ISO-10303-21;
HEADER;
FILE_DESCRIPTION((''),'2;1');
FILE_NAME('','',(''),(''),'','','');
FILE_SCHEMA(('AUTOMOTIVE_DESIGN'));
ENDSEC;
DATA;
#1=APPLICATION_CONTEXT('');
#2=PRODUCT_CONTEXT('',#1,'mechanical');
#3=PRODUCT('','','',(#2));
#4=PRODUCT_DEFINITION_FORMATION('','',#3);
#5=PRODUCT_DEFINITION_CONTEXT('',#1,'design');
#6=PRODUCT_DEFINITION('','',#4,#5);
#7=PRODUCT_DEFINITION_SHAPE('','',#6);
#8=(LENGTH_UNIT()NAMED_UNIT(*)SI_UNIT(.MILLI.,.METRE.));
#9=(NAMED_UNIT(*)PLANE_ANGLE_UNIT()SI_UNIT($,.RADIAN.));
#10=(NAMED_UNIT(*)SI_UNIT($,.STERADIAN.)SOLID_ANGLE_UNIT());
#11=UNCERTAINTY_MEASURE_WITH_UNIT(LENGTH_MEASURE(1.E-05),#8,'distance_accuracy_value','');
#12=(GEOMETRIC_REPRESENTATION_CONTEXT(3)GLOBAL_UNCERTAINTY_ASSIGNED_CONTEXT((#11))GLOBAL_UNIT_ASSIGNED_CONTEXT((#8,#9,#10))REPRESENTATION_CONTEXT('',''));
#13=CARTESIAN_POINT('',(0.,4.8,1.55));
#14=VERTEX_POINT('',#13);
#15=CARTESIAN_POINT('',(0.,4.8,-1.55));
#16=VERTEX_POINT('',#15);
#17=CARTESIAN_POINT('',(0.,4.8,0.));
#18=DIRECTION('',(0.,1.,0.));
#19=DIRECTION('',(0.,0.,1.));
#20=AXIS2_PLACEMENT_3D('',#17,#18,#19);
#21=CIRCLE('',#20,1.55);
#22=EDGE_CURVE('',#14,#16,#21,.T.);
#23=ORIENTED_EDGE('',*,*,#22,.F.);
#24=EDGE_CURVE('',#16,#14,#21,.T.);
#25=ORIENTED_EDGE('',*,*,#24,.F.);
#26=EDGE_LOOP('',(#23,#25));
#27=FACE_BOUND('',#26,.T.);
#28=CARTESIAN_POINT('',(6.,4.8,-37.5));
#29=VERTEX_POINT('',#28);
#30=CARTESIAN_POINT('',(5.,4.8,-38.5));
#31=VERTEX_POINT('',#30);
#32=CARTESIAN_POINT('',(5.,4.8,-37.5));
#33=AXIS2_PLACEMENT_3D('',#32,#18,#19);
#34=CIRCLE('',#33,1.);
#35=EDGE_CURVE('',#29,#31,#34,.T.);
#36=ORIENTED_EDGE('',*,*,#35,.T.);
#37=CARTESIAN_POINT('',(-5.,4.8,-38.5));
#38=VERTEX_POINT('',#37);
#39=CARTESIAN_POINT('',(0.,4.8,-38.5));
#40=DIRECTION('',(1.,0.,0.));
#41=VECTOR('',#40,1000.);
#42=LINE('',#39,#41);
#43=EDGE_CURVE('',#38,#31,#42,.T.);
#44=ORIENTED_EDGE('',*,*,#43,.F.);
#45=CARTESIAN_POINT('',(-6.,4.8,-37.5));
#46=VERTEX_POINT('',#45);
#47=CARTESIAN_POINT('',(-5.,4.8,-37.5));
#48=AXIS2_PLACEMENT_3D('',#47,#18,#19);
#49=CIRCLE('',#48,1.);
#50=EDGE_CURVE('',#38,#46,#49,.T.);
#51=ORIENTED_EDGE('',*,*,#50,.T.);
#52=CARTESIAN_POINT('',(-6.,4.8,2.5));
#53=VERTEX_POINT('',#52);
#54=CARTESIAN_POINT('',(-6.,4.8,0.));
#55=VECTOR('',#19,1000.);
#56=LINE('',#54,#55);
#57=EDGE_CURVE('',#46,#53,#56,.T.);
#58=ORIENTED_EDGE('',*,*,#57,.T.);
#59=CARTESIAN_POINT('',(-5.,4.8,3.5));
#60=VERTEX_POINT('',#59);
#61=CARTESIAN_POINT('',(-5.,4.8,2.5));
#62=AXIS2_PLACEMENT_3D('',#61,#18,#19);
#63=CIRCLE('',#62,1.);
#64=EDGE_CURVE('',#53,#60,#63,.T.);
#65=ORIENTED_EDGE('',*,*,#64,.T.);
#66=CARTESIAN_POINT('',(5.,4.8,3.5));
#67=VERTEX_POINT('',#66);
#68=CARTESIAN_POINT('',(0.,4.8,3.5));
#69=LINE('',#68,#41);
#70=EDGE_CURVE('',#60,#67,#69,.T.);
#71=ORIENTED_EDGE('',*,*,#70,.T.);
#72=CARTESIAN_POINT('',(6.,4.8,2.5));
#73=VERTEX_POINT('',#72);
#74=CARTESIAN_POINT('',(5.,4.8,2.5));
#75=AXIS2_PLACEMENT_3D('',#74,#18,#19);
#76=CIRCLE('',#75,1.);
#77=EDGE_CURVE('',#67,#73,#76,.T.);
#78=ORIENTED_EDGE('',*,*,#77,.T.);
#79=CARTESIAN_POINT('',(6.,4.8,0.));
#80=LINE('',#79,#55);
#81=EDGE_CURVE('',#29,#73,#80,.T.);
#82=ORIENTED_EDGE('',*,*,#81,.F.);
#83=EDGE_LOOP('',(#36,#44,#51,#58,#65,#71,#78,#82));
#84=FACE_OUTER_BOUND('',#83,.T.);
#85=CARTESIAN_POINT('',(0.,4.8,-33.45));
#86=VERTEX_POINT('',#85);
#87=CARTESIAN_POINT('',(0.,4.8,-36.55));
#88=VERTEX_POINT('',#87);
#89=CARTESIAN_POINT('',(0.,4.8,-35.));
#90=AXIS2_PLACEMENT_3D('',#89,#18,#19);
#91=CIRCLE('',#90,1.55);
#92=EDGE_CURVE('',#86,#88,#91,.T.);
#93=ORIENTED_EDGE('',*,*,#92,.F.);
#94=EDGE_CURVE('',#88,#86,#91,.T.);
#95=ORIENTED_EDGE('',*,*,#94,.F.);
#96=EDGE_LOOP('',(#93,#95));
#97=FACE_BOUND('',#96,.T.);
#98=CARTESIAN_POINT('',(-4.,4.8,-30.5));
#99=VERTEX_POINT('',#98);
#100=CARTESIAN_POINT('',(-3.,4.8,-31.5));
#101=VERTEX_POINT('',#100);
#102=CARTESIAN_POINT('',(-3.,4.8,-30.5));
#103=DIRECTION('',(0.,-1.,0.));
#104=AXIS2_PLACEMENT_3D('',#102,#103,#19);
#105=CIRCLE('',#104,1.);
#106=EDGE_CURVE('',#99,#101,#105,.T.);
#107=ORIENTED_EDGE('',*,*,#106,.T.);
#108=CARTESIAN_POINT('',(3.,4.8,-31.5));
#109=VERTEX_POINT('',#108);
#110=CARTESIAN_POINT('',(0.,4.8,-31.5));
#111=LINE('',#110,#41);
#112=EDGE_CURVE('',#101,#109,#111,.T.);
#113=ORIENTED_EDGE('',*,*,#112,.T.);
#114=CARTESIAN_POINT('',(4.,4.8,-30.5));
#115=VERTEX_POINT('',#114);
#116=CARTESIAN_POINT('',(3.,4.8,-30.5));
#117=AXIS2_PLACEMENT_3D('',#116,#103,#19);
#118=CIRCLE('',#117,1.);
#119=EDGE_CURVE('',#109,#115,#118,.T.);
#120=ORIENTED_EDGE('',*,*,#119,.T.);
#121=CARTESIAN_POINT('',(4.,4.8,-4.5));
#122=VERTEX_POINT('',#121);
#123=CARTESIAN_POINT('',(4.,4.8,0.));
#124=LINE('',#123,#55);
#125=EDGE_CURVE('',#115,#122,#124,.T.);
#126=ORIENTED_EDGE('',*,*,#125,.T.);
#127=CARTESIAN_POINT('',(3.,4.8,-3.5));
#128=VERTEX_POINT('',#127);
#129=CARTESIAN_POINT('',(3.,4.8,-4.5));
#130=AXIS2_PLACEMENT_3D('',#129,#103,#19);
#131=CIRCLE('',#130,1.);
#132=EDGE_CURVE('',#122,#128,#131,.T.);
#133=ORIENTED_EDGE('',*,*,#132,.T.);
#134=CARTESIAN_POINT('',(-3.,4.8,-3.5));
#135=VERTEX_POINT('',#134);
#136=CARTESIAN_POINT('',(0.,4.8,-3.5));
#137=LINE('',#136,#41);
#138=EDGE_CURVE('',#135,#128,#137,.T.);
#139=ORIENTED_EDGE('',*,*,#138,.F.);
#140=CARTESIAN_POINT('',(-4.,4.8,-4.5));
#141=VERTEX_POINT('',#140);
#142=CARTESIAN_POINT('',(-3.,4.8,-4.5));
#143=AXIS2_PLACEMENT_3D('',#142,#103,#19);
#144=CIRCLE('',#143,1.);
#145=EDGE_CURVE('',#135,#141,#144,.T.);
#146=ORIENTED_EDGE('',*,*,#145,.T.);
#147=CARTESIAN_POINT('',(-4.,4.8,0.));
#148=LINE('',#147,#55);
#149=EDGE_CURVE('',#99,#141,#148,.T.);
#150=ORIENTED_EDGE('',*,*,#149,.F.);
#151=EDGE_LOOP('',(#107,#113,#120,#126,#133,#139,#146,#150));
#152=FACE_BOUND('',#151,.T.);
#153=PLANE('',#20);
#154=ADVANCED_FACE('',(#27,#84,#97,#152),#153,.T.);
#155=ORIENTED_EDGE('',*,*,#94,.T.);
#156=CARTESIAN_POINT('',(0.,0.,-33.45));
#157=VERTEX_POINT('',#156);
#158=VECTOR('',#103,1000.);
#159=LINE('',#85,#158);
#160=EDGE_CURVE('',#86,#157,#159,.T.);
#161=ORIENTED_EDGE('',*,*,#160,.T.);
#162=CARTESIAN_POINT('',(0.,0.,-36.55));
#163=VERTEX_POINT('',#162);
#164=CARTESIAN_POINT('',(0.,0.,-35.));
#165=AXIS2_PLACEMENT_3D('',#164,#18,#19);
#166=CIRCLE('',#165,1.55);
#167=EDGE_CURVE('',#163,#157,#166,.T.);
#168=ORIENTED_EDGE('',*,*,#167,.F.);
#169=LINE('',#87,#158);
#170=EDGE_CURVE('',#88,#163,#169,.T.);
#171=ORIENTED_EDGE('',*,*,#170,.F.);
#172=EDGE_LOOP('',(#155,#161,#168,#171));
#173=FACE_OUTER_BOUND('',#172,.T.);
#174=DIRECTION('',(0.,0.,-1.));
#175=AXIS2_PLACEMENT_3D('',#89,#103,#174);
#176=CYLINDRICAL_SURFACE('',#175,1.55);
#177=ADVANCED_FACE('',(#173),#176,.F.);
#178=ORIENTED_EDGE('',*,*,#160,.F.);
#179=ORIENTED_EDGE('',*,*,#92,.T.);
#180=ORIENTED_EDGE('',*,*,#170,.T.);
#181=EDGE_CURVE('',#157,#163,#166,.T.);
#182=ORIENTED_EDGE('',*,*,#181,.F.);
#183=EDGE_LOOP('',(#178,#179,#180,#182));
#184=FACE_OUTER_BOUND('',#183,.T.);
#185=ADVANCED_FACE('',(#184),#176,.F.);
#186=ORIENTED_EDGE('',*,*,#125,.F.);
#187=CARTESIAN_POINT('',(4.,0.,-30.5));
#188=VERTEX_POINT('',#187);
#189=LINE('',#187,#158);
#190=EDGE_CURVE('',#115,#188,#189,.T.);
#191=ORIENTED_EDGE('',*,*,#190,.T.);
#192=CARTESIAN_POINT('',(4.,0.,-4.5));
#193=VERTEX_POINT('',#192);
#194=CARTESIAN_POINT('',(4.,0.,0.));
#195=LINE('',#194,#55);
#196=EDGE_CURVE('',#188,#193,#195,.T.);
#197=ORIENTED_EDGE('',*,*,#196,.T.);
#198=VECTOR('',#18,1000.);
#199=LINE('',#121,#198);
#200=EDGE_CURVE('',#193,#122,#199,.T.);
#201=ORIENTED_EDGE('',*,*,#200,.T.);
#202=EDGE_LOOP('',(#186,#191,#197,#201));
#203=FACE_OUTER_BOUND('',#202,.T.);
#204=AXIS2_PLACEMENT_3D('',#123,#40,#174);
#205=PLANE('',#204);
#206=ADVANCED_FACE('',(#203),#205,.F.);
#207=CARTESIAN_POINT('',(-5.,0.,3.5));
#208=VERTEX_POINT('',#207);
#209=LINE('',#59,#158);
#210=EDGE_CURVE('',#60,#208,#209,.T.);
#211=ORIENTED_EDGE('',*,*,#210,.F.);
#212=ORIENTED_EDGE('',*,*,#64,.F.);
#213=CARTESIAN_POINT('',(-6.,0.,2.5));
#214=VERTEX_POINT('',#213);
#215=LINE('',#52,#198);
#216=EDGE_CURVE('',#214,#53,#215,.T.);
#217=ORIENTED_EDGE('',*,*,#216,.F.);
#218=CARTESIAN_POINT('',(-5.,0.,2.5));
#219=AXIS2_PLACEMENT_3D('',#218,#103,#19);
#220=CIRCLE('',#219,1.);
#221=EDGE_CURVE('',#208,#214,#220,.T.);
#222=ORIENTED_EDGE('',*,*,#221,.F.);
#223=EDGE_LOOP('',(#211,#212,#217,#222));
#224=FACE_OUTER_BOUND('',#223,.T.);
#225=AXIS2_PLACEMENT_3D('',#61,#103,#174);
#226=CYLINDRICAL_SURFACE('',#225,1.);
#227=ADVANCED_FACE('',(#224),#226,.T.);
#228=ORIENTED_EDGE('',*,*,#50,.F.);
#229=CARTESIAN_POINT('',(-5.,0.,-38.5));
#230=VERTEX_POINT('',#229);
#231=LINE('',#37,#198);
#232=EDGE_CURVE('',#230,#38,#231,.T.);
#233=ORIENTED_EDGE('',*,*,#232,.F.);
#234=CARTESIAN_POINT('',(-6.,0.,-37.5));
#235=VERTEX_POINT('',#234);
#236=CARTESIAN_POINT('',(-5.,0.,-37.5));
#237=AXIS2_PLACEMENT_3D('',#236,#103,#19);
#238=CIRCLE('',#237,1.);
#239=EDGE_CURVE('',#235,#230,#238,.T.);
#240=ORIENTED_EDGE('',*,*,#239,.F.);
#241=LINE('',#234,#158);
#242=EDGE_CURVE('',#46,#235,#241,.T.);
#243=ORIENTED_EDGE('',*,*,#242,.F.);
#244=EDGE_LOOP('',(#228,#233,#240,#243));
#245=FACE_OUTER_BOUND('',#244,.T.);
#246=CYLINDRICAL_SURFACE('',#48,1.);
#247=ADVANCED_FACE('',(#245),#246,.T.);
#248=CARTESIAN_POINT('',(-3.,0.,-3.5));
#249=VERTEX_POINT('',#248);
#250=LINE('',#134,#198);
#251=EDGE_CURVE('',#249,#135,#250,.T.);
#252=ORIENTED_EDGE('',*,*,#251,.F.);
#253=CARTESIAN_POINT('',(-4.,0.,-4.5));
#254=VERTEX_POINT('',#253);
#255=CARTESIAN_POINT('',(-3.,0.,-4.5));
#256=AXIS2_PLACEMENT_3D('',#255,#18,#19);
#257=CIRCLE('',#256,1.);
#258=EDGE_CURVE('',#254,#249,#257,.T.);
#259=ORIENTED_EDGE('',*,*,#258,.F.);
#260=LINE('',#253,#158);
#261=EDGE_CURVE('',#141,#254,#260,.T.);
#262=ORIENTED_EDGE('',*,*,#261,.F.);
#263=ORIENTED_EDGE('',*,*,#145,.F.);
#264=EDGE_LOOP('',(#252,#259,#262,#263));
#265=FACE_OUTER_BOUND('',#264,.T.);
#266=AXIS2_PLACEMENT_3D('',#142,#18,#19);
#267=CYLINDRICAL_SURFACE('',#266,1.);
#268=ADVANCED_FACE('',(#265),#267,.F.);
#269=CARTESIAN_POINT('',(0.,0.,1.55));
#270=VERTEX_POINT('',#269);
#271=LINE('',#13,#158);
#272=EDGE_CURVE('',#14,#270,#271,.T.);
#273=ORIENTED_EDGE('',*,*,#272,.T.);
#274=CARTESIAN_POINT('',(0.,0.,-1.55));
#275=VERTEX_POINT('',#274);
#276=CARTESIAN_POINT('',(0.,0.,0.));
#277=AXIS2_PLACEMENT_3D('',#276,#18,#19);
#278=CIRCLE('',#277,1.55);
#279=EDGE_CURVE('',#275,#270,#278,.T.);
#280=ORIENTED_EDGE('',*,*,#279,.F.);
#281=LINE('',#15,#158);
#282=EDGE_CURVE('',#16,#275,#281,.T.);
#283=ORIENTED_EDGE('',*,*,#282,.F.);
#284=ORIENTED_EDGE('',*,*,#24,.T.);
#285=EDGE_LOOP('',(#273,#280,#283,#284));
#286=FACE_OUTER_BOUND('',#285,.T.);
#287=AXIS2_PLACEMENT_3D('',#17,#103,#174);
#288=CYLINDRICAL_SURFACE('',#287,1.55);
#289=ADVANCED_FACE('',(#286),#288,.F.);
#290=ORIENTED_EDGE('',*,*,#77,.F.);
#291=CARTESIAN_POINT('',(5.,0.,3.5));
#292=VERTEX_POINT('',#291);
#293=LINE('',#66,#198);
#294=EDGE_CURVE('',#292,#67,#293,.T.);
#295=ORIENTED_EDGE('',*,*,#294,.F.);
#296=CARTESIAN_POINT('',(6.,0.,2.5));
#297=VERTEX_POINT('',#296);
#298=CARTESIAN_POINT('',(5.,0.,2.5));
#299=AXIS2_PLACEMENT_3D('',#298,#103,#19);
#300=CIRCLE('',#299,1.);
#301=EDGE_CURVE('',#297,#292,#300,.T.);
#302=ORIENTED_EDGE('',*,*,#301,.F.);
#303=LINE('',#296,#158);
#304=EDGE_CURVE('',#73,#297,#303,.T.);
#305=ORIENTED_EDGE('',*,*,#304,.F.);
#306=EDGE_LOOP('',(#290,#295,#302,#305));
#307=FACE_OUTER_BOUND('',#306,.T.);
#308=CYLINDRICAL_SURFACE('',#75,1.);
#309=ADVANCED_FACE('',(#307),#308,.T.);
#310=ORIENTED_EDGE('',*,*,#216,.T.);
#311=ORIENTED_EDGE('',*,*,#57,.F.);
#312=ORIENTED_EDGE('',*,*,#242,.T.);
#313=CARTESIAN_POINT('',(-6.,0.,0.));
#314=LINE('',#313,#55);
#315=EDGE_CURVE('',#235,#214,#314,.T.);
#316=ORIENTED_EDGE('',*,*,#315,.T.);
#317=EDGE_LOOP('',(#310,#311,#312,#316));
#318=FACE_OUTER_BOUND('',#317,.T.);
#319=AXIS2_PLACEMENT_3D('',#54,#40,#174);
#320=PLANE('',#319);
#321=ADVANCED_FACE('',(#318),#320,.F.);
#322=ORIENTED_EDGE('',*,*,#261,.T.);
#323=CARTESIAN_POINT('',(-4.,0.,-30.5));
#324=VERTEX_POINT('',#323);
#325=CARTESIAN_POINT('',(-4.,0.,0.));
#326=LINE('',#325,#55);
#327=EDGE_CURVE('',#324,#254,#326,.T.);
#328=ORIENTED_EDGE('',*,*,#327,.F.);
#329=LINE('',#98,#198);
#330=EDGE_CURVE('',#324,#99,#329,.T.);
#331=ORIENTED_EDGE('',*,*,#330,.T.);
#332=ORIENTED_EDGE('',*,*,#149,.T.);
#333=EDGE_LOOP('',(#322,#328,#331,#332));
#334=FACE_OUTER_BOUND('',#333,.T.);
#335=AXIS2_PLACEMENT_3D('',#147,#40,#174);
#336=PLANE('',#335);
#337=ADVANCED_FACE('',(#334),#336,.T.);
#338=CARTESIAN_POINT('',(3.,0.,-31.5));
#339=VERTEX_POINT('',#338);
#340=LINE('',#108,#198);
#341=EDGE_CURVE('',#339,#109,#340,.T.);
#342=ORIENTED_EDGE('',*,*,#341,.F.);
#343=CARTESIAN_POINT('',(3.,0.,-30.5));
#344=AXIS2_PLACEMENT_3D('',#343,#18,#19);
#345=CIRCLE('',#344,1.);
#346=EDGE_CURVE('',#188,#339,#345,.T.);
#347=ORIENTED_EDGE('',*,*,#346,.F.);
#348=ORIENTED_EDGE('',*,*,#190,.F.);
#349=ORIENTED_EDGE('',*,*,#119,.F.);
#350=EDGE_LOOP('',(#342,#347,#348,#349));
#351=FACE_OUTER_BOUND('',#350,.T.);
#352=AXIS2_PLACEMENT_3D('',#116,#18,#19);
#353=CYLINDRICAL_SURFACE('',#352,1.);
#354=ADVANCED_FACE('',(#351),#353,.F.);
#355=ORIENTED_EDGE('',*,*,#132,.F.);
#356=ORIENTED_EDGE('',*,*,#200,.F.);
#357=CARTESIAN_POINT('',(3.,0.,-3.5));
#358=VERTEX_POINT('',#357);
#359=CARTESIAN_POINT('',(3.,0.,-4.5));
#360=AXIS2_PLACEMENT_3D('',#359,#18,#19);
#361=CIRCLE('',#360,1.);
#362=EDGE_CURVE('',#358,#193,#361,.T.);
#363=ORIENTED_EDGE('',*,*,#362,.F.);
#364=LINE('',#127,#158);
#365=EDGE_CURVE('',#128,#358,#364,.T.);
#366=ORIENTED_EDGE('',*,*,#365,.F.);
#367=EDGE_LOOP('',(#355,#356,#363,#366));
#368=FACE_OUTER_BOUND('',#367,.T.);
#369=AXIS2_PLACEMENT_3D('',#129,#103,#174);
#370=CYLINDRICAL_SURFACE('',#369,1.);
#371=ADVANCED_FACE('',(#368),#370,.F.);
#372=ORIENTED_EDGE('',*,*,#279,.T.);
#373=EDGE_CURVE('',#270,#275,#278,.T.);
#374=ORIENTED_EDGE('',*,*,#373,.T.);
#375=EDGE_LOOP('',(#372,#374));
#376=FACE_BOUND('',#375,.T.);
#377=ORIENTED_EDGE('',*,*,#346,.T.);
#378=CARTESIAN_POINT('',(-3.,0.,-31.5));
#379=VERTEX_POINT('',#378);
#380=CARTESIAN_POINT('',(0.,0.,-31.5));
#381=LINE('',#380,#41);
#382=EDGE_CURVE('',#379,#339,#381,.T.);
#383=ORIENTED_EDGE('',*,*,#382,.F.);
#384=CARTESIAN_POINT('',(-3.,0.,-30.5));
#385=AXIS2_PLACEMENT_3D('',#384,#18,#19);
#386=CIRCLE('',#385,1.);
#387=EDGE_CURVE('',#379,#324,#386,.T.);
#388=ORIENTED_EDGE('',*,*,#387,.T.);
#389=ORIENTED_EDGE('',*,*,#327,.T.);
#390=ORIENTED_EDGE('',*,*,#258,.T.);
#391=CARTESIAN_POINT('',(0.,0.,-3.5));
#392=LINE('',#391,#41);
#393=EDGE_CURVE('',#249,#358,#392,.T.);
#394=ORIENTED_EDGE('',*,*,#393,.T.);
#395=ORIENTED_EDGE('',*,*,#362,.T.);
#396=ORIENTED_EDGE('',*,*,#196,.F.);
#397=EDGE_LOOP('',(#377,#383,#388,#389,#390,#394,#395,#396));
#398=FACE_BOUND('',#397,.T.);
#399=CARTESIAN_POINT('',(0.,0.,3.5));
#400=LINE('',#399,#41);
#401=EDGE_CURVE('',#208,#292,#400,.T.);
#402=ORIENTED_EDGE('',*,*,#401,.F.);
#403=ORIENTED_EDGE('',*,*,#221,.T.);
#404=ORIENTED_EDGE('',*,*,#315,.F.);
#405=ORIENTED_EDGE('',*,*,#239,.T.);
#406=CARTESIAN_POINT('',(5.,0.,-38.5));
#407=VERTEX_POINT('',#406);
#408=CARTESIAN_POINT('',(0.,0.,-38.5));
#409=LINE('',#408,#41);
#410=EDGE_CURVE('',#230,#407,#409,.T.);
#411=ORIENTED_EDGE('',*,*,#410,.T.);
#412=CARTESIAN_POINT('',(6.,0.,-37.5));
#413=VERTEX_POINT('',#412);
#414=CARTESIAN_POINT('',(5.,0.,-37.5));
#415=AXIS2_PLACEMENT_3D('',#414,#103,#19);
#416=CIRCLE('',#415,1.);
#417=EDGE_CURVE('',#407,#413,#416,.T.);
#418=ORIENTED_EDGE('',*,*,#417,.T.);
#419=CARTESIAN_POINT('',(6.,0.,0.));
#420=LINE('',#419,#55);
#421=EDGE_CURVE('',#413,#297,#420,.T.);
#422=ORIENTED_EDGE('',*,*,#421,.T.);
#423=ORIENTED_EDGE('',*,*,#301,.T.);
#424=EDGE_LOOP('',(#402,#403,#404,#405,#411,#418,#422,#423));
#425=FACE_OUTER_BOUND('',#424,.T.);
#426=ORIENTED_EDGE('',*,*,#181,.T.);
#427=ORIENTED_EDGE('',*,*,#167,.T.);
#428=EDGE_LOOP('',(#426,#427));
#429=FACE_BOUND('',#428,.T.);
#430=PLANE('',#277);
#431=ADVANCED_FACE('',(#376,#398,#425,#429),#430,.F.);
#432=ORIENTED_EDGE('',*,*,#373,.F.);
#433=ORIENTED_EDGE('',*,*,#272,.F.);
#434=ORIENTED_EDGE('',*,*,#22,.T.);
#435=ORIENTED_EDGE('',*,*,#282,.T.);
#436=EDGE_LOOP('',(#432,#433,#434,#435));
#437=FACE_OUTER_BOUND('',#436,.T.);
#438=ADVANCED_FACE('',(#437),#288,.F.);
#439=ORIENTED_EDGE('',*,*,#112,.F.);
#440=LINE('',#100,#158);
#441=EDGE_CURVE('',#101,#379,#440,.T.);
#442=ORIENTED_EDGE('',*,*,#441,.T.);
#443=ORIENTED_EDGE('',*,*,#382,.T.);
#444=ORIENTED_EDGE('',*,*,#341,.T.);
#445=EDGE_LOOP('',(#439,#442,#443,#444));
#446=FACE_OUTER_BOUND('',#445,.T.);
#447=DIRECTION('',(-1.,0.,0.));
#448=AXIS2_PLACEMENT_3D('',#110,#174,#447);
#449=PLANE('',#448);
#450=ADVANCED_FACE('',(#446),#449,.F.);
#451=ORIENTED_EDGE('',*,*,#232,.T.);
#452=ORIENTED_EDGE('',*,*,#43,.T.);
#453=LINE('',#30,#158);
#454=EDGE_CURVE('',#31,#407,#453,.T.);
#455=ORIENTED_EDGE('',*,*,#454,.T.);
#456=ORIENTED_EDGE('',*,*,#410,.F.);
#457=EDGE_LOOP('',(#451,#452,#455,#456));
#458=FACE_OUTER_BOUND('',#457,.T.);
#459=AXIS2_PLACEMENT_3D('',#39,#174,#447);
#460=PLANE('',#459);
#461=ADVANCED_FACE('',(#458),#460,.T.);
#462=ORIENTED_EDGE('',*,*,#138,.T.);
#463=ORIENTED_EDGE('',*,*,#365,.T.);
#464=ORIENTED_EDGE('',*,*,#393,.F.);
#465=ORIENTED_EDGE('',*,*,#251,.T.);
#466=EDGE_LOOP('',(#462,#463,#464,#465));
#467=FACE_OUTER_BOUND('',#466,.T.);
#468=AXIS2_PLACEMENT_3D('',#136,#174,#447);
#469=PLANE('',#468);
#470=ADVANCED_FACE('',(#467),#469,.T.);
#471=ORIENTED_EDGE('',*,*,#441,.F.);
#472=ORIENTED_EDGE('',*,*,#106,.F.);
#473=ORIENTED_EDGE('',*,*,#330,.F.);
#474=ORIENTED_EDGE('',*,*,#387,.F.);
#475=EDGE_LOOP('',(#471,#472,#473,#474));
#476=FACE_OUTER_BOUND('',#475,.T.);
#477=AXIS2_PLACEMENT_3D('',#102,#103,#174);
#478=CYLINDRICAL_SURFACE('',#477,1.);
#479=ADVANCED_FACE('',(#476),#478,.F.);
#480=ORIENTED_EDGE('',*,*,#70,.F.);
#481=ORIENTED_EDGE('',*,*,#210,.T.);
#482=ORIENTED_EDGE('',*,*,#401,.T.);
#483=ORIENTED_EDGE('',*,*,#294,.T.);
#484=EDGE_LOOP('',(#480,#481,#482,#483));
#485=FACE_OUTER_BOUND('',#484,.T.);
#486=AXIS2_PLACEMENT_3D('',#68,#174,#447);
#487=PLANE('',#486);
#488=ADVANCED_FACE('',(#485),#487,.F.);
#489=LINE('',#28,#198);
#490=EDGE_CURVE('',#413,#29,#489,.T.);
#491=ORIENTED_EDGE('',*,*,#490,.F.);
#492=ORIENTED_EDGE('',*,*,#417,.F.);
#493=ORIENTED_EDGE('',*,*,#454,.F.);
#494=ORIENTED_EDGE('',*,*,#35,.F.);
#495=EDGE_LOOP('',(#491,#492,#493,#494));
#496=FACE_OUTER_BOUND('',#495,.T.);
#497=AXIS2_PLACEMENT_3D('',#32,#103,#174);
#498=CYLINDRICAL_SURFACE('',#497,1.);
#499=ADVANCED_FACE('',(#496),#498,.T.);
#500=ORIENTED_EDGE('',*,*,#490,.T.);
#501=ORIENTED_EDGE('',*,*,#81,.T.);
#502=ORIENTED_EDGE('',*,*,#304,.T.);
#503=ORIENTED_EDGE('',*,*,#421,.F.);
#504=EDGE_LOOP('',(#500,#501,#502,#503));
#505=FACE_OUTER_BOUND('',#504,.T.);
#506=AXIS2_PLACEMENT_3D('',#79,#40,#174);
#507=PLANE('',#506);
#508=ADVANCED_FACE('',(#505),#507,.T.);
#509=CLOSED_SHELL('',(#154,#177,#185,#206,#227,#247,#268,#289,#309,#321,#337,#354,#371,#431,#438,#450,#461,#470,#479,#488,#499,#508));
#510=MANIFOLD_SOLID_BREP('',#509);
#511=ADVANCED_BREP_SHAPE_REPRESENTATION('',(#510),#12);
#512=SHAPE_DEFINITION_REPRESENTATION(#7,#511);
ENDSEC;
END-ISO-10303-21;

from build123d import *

# Parameters (mm, degrees)
SKETCH_1_W      = 2
SKETCH_1_H      = 28
SKETCH_1_W_2    = 12
SKETCH_1_H_2    = 7
SKETCH_1_R      = 1.55
EXTRUDE_1_DEPTH = 4.8
FILLET_1_R      = 1


with BuildPart() as part:
    # 草图1 → 凸台-拉伸1 (new body)
    # profile 1 of 4: a face of its own
    with BuildSketch(Plane(origin=(0, 0, 0), x_dir=(1, 0, 0), z_dir=(0, 1, 0))):
        with Locations((-5, 17.5)):
            Rectangle(SKETCH_1_W, SKETCH_1_H)
    # profile 2 of 4: a face of its own
    with BuildSketch(Plane(origin=(0, 0, 0), x_dir=(1, 0, 0), z_dir=(0, 1, 0))):
        with Locations((0, 35)):
            Rectangle(SKETCH_1_W_2, SKETCH_1_H_2)
        with Locations(Location((0, 35, 0), (0, 0, 270))):
            Circle(SKETCH_1_R, mode=Mode.SUBTRACT)
    # profile 3 of 4: a face of its own
    with BuildSketch(Plane(origin=(0, 0, 0), x_dir=(1, 0, 0), z_dir=(0, 1, 0))):
        with Locations((5, 17.5)):
            Rectangle(SKETCH_1_W, SKETCH_1_H)
    # profile 4 of 4: a face of its own
    with BuildSketch(Plane(origin=(0, 0, 0), x_dir=(1, 0, 0), z_dir=(0, 1, 0))):
        Rectangle(SKETCH_1_W_2, SKETCH_1_H_2)
        with Locations(Location((0, 0, 0), (0, 0, 270))):
            Circle(SKETCH_1_R, mode=Mode.SUBTRACT)
    extrude(amount=EXTRUDE_1_DEPTH)

    # 圆角1
    fillet_1_edges = [part.edges().sort_by_distance(p)[0] for p in [
        (-4, 2.4, -3.5),
        (4, 2.4, -3.5),
        (4, 2.4, -31.5),
        (-4, 2.4, -31.5),
        (6, 2.4, 3.5),
        (-6, 2.4, 3.5),
        (-6, 2.4, -38.5),
        (6, 2.4, -38.5),
    ]]
    fillet(fillet_1_edges, radius=FILLET_1_R)


solid = part.part
